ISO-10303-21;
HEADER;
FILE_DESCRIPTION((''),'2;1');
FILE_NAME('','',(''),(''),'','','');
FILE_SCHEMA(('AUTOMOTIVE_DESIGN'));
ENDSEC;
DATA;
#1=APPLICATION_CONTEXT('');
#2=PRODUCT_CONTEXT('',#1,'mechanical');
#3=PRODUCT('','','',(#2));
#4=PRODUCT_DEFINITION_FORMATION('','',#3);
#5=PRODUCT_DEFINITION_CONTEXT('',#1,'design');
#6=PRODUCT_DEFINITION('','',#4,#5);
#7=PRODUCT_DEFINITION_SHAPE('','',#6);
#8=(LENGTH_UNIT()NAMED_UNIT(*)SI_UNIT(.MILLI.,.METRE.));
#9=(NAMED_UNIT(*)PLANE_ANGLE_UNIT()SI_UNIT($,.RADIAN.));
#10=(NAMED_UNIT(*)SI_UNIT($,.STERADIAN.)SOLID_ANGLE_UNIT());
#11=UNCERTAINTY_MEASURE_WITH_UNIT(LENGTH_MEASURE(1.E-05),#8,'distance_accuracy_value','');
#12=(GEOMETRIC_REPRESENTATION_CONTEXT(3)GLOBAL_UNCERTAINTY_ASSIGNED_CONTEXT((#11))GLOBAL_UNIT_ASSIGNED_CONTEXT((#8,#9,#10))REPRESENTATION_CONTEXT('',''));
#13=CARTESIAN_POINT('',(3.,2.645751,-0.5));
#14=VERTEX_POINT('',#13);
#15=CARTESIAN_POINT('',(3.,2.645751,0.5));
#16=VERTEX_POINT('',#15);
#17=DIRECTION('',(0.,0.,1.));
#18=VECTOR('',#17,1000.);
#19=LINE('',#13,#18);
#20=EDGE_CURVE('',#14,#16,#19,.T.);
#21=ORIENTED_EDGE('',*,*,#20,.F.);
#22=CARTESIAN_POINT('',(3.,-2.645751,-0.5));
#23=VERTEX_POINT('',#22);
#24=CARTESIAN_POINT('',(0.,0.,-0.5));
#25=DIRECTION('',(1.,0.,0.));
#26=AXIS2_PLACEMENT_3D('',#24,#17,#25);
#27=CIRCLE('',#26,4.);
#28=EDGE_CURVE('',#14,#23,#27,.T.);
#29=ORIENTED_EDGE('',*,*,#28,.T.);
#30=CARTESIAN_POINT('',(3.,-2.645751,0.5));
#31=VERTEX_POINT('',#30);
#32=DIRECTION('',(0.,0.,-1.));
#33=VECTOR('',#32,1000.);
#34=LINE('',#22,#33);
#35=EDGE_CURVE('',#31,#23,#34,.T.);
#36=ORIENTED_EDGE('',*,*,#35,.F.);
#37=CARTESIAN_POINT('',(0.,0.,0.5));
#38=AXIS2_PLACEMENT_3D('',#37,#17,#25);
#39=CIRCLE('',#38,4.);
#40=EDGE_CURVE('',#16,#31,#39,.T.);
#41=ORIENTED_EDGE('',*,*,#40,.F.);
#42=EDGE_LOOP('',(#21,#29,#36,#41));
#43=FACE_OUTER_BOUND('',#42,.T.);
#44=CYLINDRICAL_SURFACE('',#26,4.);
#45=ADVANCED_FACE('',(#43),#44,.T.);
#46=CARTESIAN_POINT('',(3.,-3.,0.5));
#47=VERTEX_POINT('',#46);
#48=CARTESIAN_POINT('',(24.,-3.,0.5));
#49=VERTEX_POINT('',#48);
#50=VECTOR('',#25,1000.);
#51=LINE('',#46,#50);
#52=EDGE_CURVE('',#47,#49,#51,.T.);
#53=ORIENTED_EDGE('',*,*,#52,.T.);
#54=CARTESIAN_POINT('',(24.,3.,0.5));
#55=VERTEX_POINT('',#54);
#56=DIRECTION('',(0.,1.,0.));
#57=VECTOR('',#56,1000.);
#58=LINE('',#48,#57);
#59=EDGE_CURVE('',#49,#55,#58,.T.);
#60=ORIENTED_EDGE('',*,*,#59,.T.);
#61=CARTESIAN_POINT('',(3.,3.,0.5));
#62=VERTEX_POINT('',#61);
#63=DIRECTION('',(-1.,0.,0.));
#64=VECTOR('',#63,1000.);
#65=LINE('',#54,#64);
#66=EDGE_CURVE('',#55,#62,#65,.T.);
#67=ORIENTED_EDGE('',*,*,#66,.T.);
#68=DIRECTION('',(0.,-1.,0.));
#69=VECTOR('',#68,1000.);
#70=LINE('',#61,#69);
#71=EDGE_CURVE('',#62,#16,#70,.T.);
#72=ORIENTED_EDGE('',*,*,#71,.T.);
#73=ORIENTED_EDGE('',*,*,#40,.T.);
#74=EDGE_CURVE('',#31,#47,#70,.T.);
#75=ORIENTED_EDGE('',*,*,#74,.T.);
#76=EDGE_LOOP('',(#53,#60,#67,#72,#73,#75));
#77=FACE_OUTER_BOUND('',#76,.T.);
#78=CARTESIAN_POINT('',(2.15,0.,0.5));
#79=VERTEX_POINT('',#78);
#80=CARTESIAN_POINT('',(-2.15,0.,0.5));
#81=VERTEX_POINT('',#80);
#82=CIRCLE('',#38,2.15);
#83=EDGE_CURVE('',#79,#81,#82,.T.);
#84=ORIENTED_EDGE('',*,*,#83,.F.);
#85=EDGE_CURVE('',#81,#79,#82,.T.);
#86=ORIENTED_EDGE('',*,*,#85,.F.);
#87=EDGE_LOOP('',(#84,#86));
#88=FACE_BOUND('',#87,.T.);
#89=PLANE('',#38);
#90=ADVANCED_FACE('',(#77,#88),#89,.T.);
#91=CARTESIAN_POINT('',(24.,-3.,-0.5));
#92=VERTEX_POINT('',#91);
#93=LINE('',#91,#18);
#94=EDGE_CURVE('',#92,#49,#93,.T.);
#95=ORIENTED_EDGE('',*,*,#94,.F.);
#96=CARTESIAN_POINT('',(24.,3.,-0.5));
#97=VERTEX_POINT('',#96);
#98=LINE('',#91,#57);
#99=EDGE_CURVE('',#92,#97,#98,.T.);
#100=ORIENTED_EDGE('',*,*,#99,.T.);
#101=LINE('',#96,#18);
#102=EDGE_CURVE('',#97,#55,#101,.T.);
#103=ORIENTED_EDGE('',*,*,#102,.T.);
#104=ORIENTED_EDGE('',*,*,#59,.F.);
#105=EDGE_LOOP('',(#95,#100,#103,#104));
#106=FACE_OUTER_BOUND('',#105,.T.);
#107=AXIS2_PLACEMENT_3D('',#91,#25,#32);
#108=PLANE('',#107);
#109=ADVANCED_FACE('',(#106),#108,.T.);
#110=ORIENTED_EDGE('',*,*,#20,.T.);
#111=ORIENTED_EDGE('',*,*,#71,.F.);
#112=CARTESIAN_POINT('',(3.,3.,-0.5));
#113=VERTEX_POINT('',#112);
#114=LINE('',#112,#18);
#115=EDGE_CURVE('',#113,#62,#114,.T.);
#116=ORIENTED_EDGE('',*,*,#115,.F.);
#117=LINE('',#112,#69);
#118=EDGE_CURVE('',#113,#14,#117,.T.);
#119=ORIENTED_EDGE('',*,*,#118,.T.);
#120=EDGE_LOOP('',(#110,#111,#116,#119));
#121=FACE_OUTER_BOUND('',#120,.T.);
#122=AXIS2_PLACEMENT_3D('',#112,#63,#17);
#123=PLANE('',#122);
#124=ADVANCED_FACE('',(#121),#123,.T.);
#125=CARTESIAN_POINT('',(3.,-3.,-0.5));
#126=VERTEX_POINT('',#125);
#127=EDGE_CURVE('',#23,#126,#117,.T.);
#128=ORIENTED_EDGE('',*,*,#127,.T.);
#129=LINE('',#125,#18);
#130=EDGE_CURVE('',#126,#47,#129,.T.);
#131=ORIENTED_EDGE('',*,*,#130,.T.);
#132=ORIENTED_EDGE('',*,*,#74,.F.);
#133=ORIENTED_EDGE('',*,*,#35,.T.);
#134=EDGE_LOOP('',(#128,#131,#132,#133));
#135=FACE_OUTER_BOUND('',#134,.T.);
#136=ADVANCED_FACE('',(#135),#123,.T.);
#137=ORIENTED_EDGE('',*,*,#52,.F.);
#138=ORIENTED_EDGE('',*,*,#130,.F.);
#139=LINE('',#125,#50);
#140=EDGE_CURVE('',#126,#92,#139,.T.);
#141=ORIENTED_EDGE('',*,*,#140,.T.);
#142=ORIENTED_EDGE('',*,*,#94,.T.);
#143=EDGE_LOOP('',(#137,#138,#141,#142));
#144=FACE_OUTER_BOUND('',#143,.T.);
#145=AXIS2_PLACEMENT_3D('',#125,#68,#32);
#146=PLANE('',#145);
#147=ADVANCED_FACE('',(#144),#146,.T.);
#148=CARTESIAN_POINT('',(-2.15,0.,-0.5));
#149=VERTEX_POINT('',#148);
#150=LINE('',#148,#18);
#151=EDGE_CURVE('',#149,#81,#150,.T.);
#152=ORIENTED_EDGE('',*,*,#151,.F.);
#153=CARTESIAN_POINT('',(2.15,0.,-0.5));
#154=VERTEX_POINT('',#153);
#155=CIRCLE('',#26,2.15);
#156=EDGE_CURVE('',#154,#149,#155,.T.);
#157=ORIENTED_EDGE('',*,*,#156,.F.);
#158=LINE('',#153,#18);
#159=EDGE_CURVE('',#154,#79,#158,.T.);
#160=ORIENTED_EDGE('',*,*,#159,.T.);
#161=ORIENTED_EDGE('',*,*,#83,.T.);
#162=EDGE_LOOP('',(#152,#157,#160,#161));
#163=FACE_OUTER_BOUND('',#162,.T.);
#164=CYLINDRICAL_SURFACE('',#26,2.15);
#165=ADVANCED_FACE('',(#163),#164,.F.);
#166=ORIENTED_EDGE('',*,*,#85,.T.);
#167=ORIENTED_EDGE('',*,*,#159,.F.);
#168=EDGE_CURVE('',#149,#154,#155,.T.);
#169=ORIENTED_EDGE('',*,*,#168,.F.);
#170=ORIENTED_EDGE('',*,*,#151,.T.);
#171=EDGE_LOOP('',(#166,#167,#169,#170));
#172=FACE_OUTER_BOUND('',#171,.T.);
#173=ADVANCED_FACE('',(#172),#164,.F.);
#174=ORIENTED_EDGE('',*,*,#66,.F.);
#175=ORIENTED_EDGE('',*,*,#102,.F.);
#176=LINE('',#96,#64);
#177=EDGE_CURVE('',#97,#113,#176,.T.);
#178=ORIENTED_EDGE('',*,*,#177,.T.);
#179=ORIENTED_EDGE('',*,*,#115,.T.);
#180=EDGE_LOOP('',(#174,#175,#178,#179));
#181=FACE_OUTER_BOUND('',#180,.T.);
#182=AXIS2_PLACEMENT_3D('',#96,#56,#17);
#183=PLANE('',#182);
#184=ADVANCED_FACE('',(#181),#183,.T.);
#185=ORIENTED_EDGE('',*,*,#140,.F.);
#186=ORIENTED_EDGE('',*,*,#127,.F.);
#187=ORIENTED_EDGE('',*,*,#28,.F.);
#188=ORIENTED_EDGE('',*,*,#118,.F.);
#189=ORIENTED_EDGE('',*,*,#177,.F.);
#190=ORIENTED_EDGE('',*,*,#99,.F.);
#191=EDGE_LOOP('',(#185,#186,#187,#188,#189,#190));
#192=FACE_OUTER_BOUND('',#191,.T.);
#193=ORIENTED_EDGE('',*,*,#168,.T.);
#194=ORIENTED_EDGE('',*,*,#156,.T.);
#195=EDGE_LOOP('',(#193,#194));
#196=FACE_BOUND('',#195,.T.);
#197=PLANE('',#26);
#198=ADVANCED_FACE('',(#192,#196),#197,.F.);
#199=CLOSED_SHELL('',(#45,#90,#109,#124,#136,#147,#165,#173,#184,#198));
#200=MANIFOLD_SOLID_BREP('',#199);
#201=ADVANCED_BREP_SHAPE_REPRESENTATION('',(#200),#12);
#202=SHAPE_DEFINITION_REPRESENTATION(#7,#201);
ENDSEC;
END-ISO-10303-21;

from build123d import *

# Parameters (mm, degrees)
SKETCH_1_R      = 4
SKETCH_1_R_2    = 2.15
EXTRUDE_1_DEPTH = 0.5
SKETCH_2_W      = 21
SKETCH_2_H      = 6
EXTRUDE_2_DEPTH = 0.5


with BuildPart() as part:
    # 草图1 → 凸台-拉伸1 (new, symmetric)
    with BuildSketch(Plane.XY):
        Circle(SKETCH_1_R)
        Circle(SKETCH_1_R_2, mode=Mode.SUBTRACT)
    extrude(amount=EXTRUDE_1_DEPTH, both=True)

    # 草图2 → 凸台-拉伸2 (add, symmetric)
    with BuildSketch(Plane.XY):
        with Locations((13.5, 0)):
            Rectangle(SKETCH_2_W, SKETCH_2_H)
    extrude(amount=EXTRUDE_2_DEPTH, both=True)


solid = part.part
